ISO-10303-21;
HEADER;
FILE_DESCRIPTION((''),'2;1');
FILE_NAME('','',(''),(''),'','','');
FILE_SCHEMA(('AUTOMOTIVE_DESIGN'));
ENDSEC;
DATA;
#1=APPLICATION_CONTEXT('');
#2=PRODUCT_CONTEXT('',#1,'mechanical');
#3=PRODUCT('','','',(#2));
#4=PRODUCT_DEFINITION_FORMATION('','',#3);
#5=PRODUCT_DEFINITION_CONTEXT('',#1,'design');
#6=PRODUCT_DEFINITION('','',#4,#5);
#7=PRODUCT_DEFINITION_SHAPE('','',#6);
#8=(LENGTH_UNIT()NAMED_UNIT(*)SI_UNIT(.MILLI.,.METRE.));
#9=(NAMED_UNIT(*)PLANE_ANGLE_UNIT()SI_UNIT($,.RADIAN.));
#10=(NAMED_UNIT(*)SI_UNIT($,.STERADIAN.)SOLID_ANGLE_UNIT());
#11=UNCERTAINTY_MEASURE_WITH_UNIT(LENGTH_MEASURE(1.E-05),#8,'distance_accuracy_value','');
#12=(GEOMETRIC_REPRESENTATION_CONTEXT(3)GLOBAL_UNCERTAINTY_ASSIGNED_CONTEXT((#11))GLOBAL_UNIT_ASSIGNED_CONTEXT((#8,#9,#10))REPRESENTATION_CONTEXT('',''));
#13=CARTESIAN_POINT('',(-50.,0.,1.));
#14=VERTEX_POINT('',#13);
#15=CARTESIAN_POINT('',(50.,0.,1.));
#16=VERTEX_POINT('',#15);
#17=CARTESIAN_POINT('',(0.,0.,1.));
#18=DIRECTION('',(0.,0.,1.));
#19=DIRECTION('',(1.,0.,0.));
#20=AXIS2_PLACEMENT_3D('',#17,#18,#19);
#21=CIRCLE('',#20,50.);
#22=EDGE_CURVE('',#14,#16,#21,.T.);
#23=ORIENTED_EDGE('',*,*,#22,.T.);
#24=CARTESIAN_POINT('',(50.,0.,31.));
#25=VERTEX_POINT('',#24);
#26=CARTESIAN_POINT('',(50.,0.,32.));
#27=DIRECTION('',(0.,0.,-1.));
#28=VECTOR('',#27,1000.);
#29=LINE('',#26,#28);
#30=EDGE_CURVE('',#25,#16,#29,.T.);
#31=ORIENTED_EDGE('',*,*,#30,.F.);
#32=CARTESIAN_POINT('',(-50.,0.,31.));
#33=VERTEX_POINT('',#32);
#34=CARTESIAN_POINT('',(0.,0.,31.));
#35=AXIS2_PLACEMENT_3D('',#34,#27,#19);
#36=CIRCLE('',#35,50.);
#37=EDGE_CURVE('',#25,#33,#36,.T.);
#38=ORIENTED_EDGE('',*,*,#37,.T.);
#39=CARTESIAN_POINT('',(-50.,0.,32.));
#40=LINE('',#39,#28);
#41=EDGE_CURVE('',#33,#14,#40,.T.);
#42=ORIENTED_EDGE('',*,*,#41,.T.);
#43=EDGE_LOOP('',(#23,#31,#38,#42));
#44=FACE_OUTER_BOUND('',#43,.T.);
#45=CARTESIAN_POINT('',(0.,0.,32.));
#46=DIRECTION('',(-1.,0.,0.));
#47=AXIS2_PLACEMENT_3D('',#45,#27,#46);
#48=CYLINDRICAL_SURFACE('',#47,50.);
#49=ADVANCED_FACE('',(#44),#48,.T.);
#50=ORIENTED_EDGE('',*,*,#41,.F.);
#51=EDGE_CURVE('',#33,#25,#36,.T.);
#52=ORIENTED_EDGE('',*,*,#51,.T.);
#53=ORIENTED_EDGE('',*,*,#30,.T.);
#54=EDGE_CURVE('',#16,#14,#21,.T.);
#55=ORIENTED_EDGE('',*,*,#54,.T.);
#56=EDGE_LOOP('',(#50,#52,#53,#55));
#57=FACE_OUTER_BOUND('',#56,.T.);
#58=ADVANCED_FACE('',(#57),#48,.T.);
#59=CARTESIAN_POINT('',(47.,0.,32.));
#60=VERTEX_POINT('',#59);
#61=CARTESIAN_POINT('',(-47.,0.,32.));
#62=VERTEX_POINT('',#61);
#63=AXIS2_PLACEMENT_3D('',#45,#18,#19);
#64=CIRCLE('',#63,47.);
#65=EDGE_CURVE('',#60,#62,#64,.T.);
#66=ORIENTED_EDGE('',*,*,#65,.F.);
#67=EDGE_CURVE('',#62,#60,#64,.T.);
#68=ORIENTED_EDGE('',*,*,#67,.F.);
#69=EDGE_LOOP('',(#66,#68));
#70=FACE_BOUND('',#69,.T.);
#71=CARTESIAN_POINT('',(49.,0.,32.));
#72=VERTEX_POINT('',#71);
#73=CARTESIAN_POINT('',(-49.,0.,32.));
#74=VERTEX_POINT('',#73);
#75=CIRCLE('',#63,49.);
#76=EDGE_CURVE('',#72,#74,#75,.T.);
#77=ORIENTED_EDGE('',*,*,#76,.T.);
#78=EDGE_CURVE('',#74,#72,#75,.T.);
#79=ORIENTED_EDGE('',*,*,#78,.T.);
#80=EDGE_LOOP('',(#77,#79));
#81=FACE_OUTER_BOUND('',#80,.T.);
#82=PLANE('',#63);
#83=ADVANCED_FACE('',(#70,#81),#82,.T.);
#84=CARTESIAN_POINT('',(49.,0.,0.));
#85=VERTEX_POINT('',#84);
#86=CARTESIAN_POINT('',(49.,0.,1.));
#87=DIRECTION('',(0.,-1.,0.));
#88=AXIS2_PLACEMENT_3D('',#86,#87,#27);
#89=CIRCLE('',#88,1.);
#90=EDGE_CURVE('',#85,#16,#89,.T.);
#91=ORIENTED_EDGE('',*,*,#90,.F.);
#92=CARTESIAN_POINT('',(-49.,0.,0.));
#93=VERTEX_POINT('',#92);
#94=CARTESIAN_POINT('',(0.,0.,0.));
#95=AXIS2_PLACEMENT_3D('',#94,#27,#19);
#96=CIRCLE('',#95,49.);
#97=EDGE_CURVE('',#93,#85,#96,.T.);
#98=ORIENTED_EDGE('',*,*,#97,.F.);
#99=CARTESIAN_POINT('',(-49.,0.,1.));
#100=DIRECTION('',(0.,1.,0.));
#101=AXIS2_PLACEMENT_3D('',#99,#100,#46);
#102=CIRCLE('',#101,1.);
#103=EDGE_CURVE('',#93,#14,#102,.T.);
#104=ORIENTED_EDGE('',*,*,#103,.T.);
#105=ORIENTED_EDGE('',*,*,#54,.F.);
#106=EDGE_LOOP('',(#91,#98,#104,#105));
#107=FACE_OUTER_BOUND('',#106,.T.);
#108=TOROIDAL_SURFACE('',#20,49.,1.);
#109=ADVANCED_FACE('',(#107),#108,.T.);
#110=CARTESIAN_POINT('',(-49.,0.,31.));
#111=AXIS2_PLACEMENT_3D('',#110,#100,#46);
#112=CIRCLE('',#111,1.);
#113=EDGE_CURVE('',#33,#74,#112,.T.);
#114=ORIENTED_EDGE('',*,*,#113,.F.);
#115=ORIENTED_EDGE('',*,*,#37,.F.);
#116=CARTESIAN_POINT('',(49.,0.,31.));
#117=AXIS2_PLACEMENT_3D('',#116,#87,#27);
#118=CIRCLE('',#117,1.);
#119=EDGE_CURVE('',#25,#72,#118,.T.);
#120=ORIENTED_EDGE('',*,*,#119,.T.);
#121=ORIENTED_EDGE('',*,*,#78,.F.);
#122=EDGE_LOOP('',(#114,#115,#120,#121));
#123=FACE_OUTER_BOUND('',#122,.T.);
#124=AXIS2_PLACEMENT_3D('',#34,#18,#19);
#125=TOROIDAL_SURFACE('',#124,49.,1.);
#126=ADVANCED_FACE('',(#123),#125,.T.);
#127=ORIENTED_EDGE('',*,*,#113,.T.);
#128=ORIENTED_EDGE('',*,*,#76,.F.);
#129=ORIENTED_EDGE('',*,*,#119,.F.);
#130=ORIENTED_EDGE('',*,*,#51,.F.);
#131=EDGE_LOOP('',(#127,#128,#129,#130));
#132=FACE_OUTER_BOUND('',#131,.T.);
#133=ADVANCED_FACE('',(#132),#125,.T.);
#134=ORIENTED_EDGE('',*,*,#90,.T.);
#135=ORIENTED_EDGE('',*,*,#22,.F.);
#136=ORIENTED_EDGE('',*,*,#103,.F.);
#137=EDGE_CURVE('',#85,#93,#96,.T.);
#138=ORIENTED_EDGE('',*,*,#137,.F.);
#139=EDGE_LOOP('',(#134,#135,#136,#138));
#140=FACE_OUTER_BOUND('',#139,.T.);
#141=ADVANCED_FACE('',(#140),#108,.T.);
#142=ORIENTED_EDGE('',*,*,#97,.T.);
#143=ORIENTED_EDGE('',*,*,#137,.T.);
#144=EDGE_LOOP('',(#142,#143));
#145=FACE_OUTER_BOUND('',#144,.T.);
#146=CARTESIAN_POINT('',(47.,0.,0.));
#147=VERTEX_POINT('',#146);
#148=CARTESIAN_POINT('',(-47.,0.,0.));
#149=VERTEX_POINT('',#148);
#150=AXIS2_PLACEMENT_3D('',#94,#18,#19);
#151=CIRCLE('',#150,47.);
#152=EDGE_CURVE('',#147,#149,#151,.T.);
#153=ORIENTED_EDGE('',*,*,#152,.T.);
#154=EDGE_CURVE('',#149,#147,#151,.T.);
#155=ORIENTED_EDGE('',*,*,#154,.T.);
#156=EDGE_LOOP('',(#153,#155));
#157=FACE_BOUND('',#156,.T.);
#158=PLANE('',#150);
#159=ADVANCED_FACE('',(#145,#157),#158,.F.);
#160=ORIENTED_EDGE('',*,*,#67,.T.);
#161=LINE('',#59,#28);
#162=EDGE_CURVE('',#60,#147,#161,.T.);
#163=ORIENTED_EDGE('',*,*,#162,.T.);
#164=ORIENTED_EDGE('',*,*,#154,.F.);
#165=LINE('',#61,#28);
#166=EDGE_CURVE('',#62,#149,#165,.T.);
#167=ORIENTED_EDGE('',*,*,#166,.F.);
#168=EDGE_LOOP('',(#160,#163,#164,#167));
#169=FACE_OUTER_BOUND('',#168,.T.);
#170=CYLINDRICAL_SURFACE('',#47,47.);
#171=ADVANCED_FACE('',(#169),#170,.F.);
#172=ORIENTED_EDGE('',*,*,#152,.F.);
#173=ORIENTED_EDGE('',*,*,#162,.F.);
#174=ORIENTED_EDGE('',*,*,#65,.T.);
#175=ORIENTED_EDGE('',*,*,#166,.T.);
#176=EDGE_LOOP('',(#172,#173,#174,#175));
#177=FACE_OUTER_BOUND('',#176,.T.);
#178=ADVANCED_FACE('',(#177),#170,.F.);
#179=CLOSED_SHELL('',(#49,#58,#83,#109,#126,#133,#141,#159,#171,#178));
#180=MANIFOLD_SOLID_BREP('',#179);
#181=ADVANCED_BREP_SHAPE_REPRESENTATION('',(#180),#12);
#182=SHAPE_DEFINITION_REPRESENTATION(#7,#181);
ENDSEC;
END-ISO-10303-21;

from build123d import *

# Parameters (mm, degrees)
SKETCH1_R           = 50
SKETCH1_R_2         = 47
BOSS_EXTRUDE1_DEPTH = 32
FILLET1_R           = 1


with BuildPart() as part:
    # Sketch1 → Boss-Extrude1 (new body)
    with BuildSketch(Plane.XY):
        Circle(SKETCH1_R)
        Circle(SKETCH1_R_2, mode=Mode.SUBTRACT)
    extrude(amount=BOSS_EXTRUDE1_DEPTH)

    # Fillet1
    fillet1_edges = [part.edges().sort_by_distance(p)[0] for p in [
        (-50, 0, 0),
        (-50, 0, 32),
    ]]
    fillet(fillet1_edges, radius=FILLET1_R)


solid = part.part
